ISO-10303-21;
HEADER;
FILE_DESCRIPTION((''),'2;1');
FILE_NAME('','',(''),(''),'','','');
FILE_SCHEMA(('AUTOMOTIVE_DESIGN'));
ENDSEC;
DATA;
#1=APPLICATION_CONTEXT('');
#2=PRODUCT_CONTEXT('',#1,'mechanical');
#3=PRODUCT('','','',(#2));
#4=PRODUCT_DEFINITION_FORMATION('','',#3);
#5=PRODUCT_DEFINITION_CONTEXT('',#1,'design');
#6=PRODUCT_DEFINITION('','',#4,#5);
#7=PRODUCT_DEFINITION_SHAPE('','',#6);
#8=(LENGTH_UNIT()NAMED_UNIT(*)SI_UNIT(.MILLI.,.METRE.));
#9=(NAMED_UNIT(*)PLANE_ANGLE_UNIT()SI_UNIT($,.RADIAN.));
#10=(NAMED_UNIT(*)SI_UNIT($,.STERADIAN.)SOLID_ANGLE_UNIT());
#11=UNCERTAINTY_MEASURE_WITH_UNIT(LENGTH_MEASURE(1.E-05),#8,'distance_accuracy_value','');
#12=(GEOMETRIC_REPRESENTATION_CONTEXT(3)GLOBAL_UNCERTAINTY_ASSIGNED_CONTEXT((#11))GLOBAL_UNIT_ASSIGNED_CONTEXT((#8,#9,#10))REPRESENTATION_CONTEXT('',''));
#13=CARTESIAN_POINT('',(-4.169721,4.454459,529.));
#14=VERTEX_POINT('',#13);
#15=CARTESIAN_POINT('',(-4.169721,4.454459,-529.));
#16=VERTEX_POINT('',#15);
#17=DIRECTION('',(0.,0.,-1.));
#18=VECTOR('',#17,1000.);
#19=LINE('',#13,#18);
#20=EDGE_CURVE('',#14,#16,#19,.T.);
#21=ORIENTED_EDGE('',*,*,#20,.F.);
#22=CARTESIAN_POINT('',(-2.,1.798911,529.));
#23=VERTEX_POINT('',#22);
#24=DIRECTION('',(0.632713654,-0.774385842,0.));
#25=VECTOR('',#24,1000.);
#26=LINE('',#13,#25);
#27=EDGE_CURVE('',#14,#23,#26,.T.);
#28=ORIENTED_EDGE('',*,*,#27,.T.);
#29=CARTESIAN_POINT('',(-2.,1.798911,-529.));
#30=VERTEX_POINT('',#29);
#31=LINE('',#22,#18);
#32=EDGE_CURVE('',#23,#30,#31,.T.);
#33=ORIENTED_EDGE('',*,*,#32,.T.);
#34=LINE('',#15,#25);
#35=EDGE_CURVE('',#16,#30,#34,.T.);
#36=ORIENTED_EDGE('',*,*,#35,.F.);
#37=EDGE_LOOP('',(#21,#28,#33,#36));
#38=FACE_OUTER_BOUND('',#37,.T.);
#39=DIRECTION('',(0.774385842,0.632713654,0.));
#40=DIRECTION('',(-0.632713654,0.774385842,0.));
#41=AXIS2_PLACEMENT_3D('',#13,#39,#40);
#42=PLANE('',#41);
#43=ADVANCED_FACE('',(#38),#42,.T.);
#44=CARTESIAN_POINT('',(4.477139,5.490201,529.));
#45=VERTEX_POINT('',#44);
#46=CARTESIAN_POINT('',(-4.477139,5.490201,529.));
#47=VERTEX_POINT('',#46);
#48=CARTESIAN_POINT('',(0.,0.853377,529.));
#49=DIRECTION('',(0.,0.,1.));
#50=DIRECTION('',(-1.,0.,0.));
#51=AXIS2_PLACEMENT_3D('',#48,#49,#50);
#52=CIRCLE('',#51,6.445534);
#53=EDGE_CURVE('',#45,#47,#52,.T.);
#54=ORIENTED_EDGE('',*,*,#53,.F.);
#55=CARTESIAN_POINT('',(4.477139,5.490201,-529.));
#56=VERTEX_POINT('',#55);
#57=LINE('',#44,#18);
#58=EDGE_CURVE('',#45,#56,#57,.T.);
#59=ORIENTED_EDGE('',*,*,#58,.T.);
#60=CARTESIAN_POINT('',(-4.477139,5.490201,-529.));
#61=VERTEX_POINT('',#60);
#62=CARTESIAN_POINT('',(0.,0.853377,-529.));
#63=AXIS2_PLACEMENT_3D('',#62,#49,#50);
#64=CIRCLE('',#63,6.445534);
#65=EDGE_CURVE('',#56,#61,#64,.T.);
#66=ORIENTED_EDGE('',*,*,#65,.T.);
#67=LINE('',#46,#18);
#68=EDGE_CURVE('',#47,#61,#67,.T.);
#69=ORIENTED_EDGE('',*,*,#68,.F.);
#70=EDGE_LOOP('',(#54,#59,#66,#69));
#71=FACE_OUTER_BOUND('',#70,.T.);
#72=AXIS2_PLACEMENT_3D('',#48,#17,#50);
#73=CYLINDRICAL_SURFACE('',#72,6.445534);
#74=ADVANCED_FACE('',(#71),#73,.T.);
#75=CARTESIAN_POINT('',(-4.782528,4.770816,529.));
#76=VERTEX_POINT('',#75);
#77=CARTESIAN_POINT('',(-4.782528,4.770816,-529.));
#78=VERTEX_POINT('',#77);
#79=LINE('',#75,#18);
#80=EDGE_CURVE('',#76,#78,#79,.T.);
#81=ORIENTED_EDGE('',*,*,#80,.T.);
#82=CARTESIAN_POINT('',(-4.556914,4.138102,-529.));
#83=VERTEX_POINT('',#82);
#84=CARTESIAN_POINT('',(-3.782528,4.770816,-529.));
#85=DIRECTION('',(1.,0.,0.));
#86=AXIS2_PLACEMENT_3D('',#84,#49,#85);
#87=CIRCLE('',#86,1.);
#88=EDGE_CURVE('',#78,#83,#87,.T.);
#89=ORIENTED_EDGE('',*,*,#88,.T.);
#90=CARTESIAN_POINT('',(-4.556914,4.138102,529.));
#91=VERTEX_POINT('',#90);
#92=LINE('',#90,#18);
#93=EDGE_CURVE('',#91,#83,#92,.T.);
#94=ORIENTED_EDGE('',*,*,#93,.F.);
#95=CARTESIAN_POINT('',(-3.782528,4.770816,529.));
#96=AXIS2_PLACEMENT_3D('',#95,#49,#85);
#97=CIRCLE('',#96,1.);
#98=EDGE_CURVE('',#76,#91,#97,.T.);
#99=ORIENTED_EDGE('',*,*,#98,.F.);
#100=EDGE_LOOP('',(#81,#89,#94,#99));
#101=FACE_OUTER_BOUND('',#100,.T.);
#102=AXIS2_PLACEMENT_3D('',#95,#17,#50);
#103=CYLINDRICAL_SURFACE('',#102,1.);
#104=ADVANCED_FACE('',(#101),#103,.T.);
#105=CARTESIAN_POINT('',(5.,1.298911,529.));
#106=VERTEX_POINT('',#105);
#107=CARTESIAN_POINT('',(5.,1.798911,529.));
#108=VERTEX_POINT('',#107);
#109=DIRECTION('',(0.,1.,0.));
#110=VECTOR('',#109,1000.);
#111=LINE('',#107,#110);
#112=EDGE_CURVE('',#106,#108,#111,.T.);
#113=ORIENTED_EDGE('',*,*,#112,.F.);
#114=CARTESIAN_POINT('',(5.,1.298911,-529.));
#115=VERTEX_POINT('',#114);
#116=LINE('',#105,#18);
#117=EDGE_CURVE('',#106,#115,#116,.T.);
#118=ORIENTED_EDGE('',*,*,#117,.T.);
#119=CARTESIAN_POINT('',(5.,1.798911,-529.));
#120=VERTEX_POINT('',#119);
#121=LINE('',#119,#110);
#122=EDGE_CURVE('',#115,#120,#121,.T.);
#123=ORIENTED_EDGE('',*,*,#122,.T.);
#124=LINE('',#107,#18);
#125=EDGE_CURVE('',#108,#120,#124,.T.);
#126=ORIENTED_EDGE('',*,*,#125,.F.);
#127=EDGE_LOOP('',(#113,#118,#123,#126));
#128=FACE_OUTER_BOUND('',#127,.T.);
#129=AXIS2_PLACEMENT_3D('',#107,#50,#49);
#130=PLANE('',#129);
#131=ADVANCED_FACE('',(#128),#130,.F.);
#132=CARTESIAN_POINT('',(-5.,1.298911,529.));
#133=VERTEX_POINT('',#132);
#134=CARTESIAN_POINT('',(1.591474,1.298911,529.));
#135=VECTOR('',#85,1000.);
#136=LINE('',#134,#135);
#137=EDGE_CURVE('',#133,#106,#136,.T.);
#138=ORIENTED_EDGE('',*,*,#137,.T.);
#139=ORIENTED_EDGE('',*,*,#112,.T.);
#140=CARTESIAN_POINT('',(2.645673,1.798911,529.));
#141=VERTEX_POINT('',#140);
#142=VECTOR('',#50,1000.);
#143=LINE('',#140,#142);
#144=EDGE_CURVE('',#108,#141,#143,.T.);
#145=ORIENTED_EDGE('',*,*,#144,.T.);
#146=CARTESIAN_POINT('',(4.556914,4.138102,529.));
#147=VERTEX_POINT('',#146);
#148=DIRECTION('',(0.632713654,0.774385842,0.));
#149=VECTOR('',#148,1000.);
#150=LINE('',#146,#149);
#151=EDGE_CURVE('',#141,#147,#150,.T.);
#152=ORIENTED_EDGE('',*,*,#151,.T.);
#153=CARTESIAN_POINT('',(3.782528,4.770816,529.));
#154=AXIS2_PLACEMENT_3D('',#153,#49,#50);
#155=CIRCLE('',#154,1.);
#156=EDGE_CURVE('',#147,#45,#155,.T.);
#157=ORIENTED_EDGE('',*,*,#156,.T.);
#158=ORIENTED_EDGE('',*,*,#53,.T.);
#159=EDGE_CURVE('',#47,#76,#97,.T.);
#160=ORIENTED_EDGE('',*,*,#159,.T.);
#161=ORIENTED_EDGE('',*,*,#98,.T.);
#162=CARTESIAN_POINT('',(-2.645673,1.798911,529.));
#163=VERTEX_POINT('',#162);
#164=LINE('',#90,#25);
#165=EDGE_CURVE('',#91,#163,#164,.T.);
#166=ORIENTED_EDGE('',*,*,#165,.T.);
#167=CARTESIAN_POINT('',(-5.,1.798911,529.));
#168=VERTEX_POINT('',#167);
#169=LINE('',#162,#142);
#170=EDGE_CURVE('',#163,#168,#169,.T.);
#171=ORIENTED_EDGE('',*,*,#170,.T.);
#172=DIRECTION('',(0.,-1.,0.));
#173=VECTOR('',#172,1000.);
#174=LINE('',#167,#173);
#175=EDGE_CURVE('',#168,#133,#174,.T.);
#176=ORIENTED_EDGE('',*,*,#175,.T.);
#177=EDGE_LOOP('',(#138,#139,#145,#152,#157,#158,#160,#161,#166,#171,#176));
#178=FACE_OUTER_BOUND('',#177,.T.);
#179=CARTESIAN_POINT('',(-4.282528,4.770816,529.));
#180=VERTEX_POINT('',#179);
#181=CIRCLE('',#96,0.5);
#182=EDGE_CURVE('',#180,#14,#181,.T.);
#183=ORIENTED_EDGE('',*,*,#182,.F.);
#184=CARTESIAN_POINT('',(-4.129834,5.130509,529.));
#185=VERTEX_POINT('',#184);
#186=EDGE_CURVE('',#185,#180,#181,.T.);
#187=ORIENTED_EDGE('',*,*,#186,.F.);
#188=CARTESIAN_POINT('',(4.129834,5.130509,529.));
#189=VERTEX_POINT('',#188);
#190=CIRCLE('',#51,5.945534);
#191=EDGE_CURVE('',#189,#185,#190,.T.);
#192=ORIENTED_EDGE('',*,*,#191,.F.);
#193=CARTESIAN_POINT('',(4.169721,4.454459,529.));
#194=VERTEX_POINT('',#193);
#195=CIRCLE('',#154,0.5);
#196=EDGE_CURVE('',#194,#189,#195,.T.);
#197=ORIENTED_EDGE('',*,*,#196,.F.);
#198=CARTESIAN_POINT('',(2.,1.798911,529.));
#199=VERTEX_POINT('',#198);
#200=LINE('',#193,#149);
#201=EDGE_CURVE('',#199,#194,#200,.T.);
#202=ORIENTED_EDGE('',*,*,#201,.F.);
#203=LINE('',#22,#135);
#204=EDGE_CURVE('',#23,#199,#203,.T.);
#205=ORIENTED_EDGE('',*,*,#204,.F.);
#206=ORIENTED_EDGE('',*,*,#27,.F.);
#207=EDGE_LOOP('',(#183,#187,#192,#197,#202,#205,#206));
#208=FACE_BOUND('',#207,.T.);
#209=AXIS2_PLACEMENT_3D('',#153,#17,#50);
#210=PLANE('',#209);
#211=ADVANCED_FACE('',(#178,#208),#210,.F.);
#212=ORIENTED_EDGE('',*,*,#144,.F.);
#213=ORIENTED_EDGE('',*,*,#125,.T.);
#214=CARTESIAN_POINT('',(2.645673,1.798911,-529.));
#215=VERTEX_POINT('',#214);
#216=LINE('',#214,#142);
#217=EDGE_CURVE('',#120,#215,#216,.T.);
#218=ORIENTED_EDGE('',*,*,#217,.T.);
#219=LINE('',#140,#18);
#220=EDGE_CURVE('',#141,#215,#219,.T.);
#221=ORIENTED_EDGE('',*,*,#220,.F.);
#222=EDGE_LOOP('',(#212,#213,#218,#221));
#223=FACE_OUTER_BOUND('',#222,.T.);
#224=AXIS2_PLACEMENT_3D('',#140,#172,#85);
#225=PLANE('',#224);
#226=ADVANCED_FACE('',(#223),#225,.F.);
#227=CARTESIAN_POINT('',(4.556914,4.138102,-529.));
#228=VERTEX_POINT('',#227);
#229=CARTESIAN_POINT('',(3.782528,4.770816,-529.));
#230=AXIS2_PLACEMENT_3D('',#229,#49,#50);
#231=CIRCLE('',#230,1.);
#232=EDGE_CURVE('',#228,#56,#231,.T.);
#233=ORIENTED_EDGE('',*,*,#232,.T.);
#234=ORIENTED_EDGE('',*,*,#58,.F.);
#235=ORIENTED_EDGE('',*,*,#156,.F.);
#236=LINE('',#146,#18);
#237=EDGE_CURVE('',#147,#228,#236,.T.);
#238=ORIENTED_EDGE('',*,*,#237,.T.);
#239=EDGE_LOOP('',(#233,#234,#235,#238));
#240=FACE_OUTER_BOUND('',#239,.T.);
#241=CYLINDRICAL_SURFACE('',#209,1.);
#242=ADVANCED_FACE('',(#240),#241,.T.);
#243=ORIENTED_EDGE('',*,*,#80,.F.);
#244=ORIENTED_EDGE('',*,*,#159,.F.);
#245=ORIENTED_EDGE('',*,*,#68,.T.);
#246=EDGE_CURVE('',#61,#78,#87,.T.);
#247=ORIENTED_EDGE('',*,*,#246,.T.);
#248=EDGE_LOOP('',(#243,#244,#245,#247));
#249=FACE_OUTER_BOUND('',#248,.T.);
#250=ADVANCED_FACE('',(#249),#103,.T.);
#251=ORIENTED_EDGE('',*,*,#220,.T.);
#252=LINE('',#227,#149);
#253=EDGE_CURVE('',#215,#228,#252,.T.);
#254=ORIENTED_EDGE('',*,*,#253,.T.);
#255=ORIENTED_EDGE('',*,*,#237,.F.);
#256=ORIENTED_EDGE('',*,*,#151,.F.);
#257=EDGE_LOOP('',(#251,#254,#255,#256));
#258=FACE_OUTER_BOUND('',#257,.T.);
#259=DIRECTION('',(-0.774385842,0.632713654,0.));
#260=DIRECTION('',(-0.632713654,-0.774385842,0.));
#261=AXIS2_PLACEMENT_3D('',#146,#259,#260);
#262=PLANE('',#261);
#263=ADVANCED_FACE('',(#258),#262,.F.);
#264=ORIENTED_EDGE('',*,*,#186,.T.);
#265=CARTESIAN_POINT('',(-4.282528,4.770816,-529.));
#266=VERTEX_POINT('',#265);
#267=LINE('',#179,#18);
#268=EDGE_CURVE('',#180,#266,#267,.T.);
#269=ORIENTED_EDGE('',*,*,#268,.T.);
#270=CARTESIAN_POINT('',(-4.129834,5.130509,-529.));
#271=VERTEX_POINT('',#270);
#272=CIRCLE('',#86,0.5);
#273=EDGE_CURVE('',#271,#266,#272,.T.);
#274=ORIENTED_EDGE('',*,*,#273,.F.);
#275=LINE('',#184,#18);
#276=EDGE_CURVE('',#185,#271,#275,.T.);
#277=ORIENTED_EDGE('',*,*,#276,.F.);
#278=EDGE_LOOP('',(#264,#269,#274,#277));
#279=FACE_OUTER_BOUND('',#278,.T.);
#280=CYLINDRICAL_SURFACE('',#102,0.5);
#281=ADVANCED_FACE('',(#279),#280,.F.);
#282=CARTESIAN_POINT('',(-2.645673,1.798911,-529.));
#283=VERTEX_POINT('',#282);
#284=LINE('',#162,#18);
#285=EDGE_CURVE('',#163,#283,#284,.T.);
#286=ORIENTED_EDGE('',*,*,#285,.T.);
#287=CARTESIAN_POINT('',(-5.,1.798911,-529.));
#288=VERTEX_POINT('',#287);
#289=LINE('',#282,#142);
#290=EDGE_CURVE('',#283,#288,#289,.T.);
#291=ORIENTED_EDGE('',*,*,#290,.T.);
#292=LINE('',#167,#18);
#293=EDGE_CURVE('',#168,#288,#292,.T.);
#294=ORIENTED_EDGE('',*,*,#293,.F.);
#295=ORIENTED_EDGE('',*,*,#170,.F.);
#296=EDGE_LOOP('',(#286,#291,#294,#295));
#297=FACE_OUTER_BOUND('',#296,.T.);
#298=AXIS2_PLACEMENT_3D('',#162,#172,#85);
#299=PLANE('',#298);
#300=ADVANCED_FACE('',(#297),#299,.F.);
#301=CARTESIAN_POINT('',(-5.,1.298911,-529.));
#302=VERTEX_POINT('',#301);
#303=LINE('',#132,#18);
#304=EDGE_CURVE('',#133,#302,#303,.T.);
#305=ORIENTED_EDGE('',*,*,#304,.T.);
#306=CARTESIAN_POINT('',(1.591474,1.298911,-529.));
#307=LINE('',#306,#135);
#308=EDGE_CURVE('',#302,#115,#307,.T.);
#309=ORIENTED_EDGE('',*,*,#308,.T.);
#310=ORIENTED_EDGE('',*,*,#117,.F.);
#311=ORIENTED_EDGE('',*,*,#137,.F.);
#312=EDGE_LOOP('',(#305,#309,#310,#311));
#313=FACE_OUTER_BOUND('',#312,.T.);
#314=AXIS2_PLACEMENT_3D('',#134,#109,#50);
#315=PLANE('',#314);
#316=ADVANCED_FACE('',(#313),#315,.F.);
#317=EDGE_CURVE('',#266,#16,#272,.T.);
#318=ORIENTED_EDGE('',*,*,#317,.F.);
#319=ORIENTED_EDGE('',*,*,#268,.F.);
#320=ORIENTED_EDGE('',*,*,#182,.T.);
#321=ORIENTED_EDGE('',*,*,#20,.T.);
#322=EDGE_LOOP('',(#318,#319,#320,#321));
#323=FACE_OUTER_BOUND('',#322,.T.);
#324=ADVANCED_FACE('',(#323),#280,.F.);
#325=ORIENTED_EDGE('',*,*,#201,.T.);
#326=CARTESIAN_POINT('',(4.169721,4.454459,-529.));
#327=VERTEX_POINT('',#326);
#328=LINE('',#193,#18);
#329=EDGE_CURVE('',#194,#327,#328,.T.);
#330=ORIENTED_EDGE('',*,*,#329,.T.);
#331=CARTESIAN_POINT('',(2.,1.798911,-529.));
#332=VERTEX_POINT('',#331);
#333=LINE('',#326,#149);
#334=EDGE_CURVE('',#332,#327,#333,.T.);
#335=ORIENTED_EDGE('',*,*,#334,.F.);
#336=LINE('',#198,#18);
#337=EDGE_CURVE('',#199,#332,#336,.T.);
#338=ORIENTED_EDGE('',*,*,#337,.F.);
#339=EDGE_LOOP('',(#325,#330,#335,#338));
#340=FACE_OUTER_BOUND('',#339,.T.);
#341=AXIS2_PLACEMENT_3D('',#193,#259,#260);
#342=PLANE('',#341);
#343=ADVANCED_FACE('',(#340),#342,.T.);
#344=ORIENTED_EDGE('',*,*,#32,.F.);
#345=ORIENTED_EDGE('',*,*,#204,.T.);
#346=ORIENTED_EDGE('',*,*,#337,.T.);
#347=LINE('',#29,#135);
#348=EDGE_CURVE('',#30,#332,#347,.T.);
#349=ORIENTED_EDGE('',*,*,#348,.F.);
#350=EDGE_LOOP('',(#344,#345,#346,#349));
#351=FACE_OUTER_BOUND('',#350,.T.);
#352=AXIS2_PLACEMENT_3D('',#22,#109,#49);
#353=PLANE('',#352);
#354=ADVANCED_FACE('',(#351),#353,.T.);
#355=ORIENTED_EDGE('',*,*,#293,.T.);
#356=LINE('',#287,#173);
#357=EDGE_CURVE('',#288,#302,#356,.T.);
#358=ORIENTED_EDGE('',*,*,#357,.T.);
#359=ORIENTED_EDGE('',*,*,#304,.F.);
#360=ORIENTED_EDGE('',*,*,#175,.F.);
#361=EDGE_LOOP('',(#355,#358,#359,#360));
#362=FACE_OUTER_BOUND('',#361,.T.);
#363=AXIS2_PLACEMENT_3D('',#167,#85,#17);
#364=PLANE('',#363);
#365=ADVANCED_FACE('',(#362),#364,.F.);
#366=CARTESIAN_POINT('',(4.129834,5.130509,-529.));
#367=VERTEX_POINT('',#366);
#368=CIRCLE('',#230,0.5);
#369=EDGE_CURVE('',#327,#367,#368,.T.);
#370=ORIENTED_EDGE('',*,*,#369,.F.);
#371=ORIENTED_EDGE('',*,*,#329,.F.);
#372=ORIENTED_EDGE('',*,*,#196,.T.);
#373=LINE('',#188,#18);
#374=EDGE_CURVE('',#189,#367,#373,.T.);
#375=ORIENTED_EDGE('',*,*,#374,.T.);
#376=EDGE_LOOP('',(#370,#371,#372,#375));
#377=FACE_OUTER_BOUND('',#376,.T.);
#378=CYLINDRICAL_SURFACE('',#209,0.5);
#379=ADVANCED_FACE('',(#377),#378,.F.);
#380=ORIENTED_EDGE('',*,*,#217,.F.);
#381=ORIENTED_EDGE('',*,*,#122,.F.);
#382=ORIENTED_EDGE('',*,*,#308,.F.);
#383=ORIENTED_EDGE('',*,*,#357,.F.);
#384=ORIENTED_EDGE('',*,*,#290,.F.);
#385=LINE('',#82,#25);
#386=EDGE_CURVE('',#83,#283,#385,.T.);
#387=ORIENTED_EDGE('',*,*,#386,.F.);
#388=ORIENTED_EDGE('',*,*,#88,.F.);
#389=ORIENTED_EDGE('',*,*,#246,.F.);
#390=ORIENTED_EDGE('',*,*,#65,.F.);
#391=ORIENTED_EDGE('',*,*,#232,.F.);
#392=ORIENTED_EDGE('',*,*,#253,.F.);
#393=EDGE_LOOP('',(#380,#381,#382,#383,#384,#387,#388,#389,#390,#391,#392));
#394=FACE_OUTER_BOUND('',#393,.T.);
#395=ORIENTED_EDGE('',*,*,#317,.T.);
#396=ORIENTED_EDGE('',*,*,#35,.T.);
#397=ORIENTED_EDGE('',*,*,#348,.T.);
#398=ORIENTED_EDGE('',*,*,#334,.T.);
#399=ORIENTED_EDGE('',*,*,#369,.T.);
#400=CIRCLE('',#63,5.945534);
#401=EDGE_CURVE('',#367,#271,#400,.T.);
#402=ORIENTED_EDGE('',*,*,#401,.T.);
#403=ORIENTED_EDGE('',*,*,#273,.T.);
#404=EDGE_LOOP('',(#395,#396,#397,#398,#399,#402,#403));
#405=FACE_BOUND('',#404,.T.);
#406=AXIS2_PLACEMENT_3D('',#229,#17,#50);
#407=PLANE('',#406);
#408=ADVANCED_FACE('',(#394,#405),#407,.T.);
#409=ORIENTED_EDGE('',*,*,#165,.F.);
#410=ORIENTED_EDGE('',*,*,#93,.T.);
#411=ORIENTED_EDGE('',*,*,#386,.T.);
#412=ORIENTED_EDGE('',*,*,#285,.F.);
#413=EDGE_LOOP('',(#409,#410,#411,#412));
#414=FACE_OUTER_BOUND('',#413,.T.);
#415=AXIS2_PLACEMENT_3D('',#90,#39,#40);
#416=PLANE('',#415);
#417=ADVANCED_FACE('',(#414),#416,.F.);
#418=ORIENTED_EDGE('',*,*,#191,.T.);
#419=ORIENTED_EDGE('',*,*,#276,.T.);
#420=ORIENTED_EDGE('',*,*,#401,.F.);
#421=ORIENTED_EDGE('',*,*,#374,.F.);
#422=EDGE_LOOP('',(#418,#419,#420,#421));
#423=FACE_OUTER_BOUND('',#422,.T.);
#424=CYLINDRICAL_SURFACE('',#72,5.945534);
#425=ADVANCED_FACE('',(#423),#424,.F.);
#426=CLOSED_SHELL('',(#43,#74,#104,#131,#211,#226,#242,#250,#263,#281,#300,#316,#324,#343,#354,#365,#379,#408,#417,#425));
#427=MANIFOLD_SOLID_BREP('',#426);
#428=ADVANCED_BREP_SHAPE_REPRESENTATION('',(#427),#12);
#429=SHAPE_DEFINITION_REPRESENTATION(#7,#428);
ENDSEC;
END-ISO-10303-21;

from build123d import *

# Parameters (mm, degrees)
EXTRUDE_1_DEPTH = 529


with BuildPart() as part:
    # 草图1 → 凸台-拉伸1 (new, symmetric)
    with BuildSketch(Plane.XY):
        with BuildLine():
            Line((-4.556913863, 4.138102128), (-2.645672962, 1.79891143))
            Line((-2.645672962, 1.79891143), (-5, 1.79891143))
            Line((-5, 1.79891143), (-5, 1.29891143))
            Line((-5, 1.29891143), (1.591473901, 1.29891143))
            Line((1.591473901, 1.29891143), (5, 1.29891143))
            Line((5, 1.29891143), (5, 1.79891143))
            Line((5, 1.79891143), (2.645672962, 1.79891143))
            Line((2.645672962, 1.79891143), (4.556913863, 4.138102128))
            ThreePointArc((4.556913863, 4.138102128), (4.780792009, 4.829714088), (4.47713902, 5.490201325))
            ThreePointArc((4.47713902, 5.490201325), (0, 7.29891143), (-4.47713902, 5.490201325))
            ThreePointArc((-4.47713902, 5.490201325), (-4.780792009, 4.829714088), (-4.556913863, 4.138102128))
        make_face()
        with BuildLine():
            Line((-2, 1.79891143), (2, 1.79891143))
            Line((2, 1.79891143), (4.169720942, 4.454458955))
            ThreePointArc((4.169720942, 4.454458955), (4.281660015, 4.800264935), (4.12983352, 5.130508554))
            ThreePointArc((4.12983352, 5.130508554), (0, 6.79891143), (-4.12983352, 5.130508554))
            ThreePointArc((-4.12983352, 5.130508554), (-4.281660015, 4.800264935), (-4.169720942, 4.454458955))
            Line((-4.169720942, 4.454458955), (-2, 1.79891143))
        make_face(mode=Mode.SUBTRACT)
    extrude(amount=EXTRUDE_1_DEPTH, both=True)


solid = part.part
